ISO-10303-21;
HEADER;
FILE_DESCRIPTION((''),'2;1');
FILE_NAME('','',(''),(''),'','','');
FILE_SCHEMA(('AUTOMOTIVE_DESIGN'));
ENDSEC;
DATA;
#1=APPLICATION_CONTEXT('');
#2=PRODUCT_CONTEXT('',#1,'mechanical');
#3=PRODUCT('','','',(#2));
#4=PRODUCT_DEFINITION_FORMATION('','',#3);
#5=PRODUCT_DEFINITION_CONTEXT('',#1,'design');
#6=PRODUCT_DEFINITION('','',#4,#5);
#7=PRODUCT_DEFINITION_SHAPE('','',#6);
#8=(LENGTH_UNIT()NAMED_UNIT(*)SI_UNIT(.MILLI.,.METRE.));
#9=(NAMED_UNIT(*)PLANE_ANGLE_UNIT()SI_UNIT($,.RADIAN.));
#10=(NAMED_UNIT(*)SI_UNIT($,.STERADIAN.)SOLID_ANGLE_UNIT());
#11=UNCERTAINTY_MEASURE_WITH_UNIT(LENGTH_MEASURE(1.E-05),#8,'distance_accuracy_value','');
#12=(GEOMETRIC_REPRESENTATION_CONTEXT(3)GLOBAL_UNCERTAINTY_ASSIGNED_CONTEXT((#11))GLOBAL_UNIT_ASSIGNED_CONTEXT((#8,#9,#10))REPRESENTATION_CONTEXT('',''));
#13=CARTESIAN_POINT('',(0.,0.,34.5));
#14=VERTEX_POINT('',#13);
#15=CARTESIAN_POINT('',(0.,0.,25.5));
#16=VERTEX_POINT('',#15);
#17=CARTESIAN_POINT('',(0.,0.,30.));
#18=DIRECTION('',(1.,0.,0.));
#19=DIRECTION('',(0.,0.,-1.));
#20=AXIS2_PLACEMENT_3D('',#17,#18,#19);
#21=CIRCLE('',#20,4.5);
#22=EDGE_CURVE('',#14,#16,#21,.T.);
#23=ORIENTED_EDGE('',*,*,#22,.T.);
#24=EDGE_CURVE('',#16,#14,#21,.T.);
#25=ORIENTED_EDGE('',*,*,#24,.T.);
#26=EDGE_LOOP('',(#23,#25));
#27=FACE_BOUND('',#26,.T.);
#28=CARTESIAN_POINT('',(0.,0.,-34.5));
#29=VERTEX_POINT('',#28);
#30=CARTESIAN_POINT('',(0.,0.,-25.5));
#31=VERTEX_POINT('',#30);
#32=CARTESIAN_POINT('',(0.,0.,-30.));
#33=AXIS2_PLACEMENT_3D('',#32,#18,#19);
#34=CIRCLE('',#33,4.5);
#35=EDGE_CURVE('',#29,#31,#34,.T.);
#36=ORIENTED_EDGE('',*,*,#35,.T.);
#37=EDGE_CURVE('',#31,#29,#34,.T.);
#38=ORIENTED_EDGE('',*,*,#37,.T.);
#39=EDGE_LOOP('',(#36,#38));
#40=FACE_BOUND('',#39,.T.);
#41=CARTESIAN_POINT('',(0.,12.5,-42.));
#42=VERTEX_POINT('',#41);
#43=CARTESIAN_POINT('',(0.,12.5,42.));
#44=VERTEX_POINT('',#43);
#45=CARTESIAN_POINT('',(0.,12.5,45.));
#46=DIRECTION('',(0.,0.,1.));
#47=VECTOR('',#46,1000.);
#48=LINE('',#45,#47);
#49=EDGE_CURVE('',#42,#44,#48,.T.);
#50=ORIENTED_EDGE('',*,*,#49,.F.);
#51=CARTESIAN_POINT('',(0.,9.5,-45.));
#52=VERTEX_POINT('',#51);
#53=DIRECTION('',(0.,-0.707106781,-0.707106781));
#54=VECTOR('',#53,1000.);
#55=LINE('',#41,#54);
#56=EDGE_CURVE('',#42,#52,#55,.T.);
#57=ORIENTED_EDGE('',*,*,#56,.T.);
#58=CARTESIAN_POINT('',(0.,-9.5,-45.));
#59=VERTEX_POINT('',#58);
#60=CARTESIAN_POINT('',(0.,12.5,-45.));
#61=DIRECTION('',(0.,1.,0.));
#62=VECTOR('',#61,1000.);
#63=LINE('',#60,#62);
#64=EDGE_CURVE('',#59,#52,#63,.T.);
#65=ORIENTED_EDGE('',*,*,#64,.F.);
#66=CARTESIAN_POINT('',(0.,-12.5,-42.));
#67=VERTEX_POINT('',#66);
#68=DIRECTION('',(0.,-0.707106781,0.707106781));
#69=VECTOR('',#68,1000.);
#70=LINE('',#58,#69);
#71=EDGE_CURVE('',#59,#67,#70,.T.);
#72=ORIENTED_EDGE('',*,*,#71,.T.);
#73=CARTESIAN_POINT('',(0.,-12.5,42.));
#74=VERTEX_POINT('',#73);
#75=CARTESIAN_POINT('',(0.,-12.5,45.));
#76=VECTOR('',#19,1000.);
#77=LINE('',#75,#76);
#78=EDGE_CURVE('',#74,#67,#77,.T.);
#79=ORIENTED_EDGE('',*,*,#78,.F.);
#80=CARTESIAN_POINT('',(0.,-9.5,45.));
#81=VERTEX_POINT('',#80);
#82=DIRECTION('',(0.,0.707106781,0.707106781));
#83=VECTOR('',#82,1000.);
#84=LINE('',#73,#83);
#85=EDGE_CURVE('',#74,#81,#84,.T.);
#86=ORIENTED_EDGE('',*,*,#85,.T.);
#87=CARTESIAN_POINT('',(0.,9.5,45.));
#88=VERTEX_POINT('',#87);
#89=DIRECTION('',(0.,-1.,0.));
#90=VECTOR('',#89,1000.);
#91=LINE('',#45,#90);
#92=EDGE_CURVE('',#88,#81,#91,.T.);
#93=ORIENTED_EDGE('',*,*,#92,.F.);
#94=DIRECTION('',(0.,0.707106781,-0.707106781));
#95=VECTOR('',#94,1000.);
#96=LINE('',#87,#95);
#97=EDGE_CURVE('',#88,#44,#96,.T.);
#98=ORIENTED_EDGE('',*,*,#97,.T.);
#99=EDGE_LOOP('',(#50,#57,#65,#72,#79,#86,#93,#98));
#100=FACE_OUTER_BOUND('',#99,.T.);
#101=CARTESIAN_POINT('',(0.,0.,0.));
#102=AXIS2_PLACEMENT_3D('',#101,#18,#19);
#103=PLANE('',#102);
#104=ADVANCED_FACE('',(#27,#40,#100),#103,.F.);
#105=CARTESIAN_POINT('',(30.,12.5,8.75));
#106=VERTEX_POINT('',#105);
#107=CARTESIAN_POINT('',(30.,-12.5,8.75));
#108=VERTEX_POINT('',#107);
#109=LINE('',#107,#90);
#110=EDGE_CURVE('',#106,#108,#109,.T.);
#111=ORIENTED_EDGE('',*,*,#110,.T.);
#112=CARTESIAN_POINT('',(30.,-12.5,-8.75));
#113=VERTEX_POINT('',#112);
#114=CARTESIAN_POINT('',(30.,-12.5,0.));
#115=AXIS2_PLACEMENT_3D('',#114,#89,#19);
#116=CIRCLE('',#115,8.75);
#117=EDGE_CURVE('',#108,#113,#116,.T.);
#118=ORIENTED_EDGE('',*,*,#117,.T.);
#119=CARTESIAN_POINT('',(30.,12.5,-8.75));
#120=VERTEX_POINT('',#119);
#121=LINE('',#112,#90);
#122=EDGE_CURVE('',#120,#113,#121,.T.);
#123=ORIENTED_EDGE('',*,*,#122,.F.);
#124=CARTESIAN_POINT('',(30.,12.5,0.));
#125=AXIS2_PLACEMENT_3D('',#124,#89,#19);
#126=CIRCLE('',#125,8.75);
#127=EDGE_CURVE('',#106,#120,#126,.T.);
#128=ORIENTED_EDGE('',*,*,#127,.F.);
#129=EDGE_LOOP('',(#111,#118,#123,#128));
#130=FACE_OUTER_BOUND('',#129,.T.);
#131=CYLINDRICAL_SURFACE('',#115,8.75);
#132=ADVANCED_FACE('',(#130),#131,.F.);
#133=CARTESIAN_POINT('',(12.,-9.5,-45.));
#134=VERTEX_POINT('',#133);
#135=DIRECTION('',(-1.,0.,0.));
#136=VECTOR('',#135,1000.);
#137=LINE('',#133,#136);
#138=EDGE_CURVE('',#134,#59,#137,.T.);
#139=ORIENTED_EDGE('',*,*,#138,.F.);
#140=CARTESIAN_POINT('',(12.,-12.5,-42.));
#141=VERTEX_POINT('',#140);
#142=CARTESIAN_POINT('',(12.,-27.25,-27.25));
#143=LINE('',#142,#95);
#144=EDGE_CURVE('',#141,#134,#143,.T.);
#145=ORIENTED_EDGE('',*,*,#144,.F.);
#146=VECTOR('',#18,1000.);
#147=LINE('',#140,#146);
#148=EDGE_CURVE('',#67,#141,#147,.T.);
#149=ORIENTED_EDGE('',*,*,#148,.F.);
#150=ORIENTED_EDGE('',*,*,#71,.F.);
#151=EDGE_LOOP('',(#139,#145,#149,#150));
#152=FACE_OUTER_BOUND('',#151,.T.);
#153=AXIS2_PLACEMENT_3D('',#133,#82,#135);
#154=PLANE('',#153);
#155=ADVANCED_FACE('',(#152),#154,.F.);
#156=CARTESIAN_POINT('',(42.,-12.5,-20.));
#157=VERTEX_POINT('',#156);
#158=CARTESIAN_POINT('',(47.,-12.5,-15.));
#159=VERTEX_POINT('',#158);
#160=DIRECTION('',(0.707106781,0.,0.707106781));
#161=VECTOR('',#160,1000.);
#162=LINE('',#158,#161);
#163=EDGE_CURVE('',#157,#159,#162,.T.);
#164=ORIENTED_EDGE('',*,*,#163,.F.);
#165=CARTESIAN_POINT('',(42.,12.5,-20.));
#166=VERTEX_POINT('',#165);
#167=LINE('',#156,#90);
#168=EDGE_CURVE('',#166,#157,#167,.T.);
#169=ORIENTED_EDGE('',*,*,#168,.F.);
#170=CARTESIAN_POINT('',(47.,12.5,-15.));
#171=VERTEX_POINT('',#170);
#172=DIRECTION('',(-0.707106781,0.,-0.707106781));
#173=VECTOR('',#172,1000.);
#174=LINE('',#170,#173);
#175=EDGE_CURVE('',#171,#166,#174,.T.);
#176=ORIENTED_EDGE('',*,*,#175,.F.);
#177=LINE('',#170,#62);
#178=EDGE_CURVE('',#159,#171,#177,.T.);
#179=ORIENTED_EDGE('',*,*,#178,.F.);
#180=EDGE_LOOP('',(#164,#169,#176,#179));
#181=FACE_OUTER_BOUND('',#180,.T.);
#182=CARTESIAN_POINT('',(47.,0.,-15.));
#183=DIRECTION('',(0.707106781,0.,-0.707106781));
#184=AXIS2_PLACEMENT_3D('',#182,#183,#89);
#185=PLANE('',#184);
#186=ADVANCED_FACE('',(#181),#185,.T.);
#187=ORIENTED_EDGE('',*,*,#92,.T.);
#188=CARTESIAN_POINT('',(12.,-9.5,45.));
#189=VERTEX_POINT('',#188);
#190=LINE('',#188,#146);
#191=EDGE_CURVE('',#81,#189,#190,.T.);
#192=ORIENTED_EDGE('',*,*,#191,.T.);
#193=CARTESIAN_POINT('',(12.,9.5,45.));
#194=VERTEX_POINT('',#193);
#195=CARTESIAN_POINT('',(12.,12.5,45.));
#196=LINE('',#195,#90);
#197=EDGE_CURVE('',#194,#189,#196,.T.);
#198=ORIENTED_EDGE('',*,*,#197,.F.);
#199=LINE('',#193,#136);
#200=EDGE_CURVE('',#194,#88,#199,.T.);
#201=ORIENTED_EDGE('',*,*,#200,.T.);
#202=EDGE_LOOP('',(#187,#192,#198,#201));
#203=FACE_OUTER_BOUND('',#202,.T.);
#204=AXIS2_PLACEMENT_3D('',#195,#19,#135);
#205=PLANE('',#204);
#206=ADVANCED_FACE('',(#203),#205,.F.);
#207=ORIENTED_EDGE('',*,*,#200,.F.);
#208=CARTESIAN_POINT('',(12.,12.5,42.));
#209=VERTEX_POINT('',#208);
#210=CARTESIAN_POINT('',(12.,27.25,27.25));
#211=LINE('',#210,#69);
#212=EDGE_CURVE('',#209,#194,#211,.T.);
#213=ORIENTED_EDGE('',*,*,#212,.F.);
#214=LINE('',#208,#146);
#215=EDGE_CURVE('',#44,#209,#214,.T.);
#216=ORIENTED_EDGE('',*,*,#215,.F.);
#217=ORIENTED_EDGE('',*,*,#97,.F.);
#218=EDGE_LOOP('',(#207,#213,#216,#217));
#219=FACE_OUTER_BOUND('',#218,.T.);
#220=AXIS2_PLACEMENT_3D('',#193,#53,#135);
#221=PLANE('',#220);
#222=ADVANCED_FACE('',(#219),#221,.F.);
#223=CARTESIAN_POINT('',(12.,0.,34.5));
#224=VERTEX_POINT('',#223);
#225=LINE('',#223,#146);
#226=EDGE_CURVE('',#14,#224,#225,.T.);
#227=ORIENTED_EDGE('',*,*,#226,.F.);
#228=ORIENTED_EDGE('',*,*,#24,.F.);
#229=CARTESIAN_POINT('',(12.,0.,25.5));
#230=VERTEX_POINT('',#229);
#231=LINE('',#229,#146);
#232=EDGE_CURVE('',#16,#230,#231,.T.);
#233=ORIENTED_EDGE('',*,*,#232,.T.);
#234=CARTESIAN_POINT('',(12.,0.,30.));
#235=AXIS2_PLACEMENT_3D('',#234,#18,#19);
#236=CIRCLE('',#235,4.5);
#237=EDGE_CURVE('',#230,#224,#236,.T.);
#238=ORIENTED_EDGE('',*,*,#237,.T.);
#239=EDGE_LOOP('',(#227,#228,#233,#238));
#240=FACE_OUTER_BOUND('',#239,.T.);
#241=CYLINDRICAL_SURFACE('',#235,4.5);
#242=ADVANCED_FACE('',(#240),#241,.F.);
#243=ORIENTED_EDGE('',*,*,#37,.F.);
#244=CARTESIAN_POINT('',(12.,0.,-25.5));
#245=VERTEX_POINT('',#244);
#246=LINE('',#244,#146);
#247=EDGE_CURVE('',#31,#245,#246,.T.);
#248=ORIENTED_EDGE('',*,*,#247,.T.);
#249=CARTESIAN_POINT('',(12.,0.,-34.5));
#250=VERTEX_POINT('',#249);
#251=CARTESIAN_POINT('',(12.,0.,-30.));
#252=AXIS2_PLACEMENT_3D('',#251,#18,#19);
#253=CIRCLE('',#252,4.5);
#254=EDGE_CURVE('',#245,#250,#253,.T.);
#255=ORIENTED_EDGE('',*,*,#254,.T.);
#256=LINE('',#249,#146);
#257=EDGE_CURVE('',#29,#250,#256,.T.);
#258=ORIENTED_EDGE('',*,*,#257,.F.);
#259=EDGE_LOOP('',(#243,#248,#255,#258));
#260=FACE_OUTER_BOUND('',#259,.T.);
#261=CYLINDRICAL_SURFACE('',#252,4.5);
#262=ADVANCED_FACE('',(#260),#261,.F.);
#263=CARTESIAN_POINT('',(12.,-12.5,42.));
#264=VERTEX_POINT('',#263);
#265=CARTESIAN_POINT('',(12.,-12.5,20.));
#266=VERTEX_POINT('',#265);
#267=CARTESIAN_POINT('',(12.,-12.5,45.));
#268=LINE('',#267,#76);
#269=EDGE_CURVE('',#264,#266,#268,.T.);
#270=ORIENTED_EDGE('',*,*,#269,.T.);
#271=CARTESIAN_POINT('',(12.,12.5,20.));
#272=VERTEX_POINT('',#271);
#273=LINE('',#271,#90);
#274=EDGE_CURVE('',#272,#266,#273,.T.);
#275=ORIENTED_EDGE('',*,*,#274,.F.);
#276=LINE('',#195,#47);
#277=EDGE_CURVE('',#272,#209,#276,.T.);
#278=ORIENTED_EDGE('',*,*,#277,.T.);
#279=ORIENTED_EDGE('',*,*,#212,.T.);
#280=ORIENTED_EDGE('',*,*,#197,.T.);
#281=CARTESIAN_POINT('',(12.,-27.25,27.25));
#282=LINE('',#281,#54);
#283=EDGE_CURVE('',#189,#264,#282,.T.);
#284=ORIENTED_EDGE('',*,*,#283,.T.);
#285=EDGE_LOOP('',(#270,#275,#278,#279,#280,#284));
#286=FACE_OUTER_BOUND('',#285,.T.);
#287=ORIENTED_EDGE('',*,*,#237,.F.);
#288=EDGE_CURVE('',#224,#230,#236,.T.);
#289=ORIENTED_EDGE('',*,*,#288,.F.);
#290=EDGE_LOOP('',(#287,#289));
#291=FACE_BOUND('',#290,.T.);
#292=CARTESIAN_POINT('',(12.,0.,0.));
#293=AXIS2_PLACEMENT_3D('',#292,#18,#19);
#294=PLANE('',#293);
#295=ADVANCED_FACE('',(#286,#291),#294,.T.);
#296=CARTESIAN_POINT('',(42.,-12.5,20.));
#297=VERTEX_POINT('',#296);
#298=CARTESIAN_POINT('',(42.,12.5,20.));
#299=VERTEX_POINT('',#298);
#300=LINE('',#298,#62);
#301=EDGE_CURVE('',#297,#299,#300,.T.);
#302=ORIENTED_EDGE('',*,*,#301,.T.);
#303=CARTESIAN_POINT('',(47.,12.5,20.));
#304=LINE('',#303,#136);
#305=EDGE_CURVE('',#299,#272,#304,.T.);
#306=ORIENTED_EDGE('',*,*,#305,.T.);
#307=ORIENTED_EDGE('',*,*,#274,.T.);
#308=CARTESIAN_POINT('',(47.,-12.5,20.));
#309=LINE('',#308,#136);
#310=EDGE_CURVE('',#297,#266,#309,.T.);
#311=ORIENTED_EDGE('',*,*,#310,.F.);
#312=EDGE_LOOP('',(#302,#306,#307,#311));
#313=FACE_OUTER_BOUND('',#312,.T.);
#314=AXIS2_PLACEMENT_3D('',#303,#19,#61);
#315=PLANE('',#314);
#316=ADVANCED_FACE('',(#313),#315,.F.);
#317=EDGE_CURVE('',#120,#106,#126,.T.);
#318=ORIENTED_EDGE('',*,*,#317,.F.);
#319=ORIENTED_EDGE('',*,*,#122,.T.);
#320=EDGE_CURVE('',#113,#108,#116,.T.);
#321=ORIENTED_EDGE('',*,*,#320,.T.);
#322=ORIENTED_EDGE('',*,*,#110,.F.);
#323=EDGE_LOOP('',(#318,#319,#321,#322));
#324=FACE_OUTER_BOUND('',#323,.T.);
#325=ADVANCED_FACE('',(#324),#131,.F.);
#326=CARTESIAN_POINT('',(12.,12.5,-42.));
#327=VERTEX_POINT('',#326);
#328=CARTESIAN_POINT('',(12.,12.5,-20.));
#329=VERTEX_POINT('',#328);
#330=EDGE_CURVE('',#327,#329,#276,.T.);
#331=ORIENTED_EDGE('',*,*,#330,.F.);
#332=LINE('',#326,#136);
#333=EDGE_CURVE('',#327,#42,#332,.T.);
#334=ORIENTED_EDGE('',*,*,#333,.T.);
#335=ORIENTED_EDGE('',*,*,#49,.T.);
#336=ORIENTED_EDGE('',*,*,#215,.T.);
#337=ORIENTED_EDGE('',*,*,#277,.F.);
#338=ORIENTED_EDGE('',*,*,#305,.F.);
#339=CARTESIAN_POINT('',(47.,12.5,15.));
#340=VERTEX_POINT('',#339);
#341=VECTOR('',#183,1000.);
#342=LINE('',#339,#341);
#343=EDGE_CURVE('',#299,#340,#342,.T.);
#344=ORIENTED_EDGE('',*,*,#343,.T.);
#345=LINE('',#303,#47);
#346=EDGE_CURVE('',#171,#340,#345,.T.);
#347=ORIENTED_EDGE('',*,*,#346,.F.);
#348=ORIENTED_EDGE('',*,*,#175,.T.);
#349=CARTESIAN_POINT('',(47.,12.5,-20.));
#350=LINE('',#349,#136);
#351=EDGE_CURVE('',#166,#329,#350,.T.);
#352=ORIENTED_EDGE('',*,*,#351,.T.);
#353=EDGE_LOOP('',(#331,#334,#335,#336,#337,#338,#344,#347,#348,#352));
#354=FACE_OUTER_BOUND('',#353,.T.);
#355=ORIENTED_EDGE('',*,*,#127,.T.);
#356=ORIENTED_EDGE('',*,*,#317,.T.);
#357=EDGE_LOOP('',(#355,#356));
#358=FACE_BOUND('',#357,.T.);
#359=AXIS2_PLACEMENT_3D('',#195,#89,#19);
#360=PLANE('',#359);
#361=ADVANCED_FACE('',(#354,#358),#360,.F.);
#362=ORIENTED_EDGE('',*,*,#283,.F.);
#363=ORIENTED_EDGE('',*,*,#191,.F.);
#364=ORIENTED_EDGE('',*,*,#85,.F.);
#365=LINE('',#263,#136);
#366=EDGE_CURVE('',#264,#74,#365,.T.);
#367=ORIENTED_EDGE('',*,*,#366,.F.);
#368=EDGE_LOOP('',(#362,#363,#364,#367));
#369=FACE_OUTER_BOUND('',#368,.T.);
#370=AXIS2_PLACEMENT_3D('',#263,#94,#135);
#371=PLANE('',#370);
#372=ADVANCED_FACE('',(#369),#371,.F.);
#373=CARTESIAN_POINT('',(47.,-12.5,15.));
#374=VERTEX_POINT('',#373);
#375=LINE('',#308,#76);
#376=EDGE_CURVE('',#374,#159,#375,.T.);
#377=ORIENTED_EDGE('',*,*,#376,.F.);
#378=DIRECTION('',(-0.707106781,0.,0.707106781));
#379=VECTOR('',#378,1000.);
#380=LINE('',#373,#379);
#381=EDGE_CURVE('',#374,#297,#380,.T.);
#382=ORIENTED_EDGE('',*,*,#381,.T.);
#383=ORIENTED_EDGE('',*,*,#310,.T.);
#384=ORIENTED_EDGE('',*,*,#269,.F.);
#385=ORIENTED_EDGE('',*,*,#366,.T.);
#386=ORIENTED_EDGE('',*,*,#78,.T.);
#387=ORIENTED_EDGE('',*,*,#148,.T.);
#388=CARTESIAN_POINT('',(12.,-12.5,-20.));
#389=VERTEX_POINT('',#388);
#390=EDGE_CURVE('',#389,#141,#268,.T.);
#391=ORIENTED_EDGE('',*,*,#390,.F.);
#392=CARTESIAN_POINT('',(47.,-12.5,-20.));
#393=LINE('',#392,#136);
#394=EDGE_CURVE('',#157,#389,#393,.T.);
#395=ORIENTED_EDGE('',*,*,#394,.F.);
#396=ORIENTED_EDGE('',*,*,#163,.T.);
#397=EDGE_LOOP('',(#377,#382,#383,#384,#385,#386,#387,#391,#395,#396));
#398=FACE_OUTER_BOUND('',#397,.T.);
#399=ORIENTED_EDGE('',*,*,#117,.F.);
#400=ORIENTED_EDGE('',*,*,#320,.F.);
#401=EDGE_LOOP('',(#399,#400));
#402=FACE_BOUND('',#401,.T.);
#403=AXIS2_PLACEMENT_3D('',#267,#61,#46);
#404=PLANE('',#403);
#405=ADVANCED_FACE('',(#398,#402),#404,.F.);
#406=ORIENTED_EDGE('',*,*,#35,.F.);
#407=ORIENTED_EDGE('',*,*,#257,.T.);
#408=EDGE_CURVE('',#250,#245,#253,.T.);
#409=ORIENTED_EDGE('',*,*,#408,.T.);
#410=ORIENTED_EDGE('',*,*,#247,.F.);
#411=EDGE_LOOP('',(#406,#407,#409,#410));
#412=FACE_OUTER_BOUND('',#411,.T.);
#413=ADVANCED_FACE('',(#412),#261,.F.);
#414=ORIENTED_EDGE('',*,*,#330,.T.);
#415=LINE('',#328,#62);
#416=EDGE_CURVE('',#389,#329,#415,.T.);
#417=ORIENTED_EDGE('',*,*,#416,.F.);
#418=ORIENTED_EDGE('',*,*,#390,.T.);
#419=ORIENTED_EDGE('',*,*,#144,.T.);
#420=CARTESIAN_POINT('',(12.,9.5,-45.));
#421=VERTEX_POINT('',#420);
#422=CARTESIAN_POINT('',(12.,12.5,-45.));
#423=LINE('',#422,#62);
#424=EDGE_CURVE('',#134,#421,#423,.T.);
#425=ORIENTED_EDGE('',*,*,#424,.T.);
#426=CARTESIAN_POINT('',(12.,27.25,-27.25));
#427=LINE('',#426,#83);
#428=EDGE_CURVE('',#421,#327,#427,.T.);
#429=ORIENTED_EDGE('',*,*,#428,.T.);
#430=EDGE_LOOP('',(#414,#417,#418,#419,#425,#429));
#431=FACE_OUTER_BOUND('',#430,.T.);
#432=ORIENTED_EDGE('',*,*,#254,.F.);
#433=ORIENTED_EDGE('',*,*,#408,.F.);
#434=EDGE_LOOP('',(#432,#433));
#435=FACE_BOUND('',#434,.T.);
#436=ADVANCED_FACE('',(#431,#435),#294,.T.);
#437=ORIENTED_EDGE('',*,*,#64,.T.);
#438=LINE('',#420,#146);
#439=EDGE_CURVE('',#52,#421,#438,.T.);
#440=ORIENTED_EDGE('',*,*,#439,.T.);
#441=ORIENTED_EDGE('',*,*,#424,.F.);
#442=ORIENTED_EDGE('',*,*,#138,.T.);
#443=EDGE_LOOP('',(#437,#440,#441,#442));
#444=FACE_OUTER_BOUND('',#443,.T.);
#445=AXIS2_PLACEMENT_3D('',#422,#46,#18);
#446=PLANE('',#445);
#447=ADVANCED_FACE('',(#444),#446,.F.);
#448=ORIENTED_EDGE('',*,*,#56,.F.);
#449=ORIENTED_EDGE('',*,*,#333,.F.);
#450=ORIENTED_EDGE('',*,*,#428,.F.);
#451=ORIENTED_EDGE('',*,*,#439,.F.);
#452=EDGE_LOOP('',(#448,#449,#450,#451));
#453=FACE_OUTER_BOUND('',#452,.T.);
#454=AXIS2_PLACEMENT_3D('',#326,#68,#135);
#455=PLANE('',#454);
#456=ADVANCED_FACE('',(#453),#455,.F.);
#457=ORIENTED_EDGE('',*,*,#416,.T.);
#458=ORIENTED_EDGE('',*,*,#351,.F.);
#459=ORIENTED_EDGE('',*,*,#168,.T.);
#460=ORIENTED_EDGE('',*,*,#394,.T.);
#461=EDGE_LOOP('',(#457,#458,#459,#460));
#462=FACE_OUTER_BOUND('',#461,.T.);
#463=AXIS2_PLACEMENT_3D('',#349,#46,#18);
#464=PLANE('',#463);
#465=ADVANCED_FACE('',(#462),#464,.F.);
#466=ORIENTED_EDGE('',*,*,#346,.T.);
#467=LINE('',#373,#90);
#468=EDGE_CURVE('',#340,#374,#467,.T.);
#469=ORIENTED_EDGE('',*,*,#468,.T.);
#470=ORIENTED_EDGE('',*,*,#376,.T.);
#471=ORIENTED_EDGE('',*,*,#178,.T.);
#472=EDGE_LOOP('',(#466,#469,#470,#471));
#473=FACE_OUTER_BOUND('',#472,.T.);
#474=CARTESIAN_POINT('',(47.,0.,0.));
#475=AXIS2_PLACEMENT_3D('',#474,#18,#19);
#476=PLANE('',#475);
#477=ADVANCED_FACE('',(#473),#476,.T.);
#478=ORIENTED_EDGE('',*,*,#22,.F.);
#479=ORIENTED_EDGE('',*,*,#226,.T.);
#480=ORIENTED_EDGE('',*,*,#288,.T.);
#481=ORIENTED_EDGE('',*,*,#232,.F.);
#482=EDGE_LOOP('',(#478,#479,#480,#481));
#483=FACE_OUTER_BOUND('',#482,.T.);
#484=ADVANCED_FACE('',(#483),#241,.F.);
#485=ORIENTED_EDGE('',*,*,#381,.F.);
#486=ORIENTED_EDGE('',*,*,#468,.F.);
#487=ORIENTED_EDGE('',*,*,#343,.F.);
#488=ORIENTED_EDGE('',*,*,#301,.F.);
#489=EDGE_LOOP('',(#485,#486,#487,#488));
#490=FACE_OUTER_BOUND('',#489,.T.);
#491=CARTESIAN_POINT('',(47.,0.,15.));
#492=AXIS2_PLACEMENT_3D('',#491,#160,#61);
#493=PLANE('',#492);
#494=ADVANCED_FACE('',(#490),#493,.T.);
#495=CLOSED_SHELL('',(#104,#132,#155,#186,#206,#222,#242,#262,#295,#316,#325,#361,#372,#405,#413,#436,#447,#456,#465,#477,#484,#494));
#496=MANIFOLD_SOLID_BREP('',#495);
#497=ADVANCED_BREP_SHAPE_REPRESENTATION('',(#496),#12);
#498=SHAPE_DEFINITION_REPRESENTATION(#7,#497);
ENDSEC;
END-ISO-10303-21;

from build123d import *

# Parameters (mm, degrees)
SKETCH_1_W            = 90
SKETCH_1_H            = 25
EXTRUDE_1_DEPTH       = 12
SKETCH_2_W            = 40
SKETCH_2_H            = 25
EXTRUDE_2_DEPTH       = 35
HOLE_WIZARD_M20_1_D   = 17.5
HOLE_WIZARD_9_0_9_1_D = 9
CHAMFER_1_SIZE        = 5
CHAMFER_2_SIZE        = 3


with BuildPart() as part:
    # 草图1 → 凸台-拉伸1 (new body)
    with BuildSketch(Plane(origin=(0, 0, 0), x_dir=(0, 0, -1), z_dir=(1, 0, 0))):
        Rectangle(SKETCH_1_W, SKETCH_1_H)
    extrude(amount=EXTRUDE_1_DEPTH)

    # 草图2 → 凸台-拉伸2 (add)
    with BuildSketch(Plane(origin=(12, 0, 0), x_dir=(0, 0, -1), z_dir=(1, 0, 0))):
        Rectangle(SKETCH_2_W, SKETCH_2_H)
    extrude(amount=EXTRUDE_2_DEPTH)

    # M20 螺纹孔1 (through all)
    with Locations(Plane(origin=(0, -12.5, 0), x_dir=(-1, 0, 0), z_dir=(0, -1, 0))):
        with Locations((-30, 0)):
            Hole(HOLE_WIZARD_M20_1_D / 2)

    # Ø9.0 (9) 直径孔1 (through all)
    with Locations(Plane(origin=(12, 0, 0), x_dir=(0, 0, -1), z_dir=(1, 0, 0))):
        with Locations((-30, 0), (30, 0)):
            Hole(HOLE_WIZARD_9_0_9_1_D / 2)

    # 倒角1
    chamfer_1_edges = [part.edges().sort_by_distance(p)[0] for p in [
        (47, 0, -20),
        (47, 0, 20),
    ]]
    chamfer(chamfer_1_edges, length=CHAMFER_1_SIZE)

    # 倒角2
    chamfer_2_edges = [part.edges().sort_by_distance(p)[0] for p in [
        (6, -12.5, -45),
        (6, -12.5, 45),
        (6, 12.5, 45),
        (6, 12.5, -45),
    ]]
    chamfer(chamfer_2_edges, length=CHAMFER_2_SIZE)


solid = part.part
